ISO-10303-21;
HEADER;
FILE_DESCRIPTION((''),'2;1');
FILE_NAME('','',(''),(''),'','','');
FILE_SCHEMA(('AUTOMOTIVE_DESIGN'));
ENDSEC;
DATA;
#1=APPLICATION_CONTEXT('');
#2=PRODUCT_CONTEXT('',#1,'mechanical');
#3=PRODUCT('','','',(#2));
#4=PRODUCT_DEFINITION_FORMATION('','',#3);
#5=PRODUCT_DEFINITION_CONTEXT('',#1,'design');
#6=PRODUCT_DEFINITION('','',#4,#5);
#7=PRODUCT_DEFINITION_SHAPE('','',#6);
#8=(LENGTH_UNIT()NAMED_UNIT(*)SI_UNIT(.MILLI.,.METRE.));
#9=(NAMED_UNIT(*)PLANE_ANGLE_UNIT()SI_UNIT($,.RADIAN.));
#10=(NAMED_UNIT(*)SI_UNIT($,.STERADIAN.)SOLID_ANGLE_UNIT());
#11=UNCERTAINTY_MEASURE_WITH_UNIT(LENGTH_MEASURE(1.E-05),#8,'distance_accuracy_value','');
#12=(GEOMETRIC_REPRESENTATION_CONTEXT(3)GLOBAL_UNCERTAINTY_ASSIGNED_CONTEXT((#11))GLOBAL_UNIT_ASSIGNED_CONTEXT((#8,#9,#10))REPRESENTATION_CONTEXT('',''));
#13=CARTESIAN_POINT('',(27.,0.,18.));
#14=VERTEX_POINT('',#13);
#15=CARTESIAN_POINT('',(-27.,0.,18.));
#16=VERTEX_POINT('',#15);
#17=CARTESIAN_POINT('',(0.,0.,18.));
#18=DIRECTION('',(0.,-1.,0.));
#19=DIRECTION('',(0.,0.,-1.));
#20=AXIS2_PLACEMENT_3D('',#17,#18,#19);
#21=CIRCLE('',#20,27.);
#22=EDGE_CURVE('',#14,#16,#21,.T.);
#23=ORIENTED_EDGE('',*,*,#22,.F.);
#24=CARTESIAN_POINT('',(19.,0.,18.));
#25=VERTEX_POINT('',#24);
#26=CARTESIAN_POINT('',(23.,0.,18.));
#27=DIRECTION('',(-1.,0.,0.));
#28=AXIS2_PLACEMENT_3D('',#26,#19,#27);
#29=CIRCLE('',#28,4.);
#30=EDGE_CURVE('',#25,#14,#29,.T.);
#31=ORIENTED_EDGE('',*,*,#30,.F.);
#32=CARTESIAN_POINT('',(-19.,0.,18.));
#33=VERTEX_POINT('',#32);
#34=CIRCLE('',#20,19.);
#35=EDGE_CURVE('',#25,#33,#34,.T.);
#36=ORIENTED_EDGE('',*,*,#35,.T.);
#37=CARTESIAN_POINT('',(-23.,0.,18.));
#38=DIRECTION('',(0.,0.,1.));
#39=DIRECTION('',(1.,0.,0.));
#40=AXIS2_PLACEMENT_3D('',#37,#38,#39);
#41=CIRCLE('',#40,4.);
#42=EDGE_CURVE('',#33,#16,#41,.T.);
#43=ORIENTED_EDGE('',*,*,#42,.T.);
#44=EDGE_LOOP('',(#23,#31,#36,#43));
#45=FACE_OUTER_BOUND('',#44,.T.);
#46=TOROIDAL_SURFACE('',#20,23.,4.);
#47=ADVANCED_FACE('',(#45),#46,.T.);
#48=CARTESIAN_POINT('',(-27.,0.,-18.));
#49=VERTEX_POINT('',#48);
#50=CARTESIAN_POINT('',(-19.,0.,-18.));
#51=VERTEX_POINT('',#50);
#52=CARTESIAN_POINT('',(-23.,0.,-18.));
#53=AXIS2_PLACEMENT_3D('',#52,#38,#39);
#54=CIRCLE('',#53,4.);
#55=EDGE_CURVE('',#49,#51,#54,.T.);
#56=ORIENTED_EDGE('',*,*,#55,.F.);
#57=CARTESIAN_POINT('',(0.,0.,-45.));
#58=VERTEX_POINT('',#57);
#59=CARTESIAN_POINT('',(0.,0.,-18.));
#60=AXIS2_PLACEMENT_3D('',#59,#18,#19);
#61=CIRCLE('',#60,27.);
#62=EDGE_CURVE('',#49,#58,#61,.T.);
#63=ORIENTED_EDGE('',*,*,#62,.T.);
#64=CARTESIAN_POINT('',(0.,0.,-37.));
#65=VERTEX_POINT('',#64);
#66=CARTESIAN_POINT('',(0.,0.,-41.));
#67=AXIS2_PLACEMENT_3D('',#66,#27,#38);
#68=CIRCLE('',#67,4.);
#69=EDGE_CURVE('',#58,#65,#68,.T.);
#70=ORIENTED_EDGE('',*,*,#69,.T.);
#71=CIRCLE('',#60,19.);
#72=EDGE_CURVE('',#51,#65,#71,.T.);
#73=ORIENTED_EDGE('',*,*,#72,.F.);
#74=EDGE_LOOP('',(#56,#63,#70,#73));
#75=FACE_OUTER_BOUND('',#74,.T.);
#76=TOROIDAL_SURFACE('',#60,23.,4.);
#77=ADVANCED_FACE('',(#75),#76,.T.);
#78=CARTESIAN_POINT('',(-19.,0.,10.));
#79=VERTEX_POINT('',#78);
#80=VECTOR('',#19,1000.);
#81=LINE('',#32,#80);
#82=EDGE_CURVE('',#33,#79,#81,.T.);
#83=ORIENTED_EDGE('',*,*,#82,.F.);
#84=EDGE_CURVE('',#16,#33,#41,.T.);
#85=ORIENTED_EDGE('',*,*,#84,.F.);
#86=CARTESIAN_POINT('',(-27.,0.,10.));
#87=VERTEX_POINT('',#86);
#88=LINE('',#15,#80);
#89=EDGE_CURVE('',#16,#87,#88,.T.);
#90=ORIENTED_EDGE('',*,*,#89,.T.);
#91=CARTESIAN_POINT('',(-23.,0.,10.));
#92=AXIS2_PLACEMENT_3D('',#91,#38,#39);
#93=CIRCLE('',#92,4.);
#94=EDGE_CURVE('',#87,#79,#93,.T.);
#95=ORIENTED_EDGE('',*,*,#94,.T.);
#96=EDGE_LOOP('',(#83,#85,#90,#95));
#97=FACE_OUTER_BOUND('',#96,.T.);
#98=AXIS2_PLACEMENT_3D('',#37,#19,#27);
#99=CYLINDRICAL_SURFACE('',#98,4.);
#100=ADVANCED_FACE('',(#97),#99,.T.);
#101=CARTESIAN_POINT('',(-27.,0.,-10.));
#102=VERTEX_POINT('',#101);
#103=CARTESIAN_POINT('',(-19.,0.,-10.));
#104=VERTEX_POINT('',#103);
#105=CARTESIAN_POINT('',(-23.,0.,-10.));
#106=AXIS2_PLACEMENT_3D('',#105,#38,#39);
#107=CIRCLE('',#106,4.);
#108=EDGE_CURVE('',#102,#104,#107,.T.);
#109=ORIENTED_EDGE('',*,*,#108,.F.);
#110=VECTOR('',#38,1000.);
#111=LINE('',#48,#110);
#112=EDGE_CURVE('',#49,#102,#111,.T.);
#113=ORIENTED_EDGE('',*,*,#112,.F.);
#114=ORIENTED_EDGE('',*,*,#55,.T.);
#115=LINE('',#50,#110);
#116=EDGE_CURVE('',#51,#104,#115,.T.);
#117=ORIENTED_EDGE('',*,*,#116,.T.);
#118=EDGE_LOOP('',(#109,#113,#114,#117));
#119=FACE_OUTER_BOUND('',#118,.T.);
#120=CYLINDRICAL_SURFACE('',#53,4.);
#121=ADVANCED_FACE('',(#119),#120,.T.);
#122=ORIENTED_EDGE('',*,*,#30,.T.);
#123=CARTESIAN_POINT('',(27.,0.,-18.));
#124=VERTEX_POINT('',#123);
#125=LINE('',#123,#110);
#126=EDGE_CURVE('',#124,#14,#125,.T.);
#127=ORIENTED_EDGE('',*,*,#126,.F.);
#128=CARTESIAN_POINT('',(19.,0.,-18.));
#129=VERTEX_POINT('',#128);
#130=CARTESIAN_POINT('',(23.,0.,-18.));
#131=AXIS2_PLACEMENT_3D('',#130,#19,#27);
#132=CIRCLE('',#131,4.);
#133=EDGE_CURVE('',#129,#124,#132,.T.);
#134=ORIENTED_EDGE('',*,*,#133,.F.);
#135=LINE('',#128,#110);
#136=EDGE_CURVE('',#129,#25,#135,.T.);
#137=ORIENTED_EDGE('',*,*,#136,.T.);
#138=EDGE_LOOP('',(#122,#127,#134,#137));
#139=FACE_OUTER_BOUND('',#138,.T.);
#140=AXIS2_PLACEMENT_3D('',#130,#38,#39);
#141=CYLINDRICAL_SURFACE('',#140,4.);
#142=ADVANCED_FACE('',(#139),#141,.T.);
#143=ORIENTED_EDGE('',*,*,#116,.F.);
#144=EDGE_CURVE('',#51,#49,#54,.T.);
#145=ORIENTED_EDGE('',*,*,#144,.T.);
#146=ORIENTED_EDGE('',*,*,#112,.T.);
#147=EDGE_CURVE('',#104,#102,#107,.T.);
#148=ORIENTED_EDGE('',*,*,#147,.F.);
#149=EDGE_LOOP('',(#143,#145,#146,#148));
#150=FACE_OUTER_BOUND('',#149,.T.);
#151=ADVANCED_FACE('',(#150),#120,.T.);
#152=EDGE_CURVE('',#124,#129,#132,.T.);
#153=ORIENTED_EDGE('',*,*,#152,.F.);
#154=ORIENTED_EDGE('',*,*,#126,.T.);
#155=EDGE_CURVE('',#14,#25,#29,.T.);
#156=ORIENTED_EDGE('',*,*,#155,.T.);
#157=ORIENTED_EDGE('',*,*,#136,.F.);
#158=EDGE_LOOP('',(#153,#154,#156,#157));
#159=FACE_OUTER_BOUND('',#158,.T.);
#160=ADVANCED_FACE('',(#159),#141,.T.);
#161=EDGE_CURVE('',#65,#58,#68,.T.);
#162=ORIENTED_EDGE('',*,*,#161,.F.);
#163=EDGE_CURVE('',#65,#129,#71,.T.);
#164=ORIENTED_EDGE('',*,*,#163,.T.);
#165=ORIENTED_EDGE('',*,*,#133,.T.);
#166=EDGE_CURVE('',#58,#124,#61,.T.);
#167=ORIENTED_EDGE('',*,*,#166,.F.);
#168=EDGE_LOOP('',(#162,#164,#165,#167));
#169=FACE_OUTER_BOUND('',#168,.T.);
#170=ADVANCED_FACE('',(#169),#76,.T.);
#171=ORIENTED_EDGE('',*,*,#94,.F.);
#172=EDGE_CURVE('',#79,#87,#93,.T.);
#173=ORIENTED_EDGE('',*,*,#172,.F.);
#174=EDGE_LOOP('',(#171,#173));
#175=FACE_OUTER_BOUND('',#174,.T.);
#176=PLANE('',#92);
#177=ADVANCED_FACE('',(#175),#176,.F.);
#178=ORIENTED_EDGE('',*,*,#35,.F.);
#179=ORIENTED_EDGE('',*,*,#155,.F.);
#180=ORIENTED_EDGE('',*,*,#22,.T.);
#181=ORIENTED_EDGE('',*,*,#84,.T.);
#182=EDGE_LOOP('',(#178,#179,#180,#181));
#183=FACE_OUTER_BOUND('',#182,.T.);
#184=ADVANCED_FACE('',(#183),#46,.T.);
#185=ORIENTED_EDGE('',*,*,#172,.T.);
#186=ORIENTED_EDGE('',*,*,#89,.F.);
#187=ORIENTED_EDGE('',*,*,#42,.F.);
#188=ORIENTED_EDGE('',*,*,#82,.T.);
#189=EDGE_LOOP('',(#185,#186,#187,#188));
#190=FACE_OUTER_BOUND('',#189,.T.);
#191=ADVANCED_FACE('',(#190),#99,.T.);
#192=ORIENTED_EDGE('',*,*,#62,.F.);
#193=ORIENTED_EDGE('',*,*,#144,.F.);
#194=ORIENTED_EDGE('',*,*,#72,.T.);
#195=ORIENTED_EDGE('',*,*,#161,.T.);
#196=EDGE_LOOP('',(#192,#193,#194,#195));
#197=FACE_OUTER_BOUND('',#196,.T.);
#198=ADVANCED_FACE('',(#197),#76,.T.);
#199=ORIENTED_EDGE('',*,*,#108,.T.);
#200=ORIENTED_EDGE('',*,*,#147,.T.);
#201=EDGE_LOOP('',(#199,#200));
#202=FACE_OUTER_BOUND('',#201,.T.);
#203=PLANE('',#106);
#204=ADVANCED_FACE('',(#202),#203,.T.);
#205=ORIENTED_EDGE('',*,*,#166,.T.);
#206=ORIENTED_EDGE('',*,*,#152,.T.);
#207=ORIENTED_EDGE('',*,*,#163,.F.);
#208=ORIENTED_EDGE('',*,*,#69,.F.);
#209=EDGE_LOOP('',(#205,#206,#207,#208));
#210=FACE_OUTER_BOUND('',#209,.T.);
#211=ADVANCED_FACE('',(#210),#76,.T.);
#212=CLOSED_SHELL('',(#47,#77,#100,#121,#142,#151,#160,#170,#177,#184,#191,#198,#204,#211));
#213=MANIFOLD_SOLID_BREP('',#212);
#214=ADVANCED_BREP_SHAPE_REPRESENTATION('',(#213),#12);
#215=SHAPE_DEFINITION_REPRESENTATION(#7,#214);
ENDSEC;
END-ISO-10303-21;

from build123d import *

# Parameters (mm, degrees)
SKETCH2_R = 4


with BuildPart() as part:
    # Sweep1: sweep along a path in Sketch1
    with BuildLine(Plane(origin=(0, 0, 0), x_dir=(1, 0, 0), z_dir=(0, 1, 0))) as sweep1_path:
        Line((-23, 10), (-23, 18))
        ThreePointArc((-23, 18), (0, 41), (23, 18))
        Line((23, 18), (23, -18))
        ThreePointArc((23, -18), (0, -41), (-23, -18))
        Line((-23, -18), (-23, -10))
    # Sketch2 → Sweep1 (sweep)
    with BuildSketch(Plane.XY.offset(-10)):
        with Locations((-23, 0)):
            Circle(SKETCH2_R)
    sweep(path=sweep1_path.line)


solid = part.part
